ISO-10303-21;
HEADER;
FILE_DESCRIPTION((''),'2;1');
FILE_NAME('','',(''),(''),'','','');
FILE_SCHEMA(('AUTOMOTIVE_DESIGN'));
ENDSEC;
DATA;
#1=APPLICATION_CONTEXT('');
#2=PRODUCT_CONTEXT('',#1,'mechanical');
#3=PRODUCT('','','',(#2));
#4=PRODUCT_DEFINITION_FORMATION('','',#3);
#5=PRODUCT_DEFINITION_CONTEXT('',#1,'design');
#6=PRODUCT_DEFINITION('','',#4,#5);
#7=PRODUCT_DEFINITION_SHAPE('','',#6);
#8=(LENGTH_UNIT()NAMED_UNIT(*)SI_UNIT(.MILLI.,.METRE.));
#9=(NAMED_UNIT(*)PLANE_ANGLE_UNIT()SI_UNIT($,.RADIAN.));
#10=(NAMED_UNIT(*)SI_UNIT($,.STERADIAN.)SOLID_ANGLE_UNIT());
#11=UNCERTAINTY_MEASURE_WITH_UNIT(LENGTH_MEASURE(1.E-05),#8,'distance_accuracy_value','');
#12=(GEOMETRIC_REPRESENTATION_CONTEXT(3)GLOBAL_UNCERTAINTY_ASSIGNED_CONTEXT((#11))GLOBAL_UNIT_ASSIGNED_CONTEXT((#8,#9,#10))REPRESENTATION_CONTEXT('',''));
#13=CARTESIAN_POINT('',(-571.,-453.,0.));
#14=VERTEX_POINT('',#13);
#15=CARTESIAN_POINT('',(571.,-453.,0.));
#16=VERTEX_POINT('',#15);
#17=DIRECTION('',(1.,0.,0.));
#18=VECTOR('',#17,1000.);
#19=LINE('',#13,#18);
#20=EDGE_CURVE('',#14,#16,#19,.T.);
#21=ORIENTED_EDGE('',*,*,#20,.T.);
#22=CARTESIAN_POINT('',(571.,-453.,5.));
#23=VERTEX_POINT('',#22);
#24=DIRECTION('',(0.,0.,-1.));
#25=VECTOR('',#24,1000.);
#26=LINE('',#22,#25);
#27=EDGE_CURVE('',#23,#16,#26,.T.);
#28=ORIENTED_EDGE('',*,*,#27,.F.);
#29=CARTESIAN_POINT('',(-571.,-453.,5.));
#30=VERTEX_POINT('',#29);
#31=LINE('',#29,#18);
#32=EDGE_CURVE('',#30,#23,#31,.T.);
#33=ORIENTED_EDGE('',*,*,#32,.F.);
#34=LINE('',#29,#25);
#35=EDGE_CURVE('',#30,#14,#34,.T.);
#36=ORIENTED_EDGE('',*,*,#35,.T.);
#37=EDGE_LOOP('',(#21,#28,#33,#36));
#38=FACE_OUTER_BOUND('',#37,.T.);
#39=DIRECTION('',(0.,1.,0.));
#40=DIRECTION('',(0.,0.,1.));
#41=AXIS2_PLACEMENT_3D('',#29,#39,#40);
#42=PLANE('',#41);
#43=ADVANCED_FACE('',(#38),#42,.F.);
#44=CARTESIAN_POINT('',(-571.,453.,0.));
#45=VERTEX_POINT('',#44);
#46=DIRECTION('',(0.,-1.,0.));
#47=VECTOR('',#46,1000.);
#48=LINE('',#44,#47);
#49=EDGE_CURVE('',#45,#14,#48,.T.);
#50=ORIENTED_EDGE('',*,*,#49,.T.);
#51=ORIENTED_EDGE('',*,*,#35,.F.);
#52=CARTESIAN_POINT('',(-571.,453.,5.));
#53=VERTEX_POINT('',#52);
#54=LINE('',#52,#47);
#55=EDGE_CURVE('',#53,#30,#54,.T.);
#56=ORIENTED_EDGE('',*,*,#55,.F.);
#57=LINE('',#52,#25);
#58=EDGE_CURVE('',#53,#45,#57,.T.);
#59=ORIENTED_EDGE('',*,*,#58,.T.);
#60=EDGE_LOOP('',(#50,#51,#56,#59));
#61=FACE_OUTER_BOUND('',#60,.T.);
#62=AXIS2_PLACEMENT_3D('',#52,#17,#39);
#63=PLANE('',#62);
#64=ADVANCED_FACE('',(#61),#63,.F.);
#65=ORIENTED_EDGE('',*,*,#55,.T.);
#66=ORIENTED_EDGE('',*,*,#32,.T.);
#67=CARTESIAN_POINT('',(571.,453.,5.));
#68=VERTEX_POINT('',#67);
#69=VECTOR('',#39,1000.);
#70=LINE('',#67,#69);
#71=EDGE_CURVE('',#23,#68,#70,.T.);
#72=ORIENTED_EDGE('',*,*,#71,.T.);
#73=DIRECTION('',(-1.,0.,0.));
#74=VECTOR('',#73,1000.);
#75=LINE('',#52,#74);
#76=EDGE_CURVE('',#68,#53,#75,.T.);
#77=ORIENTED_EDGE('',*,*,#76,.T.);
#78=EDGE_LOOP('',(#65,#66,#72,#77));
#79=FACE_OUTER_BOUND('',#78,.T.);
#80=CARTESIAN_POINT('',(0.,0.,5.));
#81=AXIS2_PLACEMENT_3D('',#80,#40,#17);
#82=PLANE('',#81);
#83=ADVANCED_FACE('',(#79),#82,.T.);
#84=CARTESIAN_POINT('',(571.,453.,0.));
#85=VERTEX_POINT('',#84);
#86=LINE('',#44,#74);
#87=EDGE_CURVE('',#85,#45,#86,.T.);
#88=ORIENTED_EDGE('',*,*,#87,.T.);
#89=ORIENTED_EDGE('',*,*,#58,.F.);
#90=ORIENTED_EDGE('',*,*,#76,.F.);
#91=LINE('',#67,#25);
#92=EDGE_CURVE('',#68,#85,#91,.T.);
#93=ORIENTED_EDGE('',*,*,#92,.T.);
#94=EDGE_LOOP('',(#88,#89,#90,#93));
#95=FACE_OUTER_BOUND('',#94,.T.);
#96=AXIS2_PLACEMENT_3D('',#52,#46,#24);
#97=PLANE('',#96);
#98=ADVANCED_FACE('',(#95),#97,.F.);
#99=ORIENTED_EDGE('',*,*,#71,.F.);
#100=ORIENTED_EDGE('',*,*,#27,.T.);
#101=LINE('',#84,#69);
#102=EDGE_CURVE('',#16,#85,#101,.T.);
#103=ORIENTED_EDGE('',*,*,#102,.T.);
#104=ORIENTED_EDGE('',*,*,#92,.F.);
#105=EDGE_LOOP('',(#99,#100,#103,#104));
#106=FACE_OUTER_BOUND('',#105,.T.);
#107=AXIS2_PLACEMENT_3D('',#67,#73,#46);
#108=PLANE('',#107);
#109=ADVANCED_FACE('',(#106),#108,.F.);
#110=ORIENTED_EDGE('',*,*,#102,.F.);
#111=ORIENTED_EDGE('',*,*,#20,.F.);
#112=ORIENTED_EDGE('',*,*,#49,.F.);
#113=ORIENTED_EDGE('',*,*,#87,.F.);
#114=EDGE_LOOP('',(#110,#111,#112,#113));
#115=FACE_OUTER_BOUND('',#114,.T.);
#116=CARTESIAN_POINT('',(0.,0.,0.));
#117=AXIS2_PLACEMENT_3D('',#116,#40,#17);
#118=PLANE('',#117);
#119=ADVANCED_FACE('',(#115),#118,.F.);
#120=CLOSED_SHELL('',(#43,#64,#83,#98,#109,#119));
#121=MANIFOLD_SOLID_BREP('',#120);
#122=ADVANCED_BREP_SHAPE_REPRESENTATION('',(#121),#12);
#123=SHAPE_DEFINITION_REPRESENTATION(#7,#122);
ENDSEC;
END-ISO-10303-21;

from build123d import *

# Parameters (mm, degrees)
SKETCH_1_W      = 1142
SKETCH_1_H      = 906
EXTRUDE_1_DEPTH = 5


with BuildPart() as part:
    # 草图1 → 凸台-拉伸1 (new body)
    with BuildSketch(Plane.XY):
        Rectangle(SKETCH_1_W, SKETCH_1_H)
    extrude(amount=EXTRUDE_1_DEPTH)


solid = part.part
